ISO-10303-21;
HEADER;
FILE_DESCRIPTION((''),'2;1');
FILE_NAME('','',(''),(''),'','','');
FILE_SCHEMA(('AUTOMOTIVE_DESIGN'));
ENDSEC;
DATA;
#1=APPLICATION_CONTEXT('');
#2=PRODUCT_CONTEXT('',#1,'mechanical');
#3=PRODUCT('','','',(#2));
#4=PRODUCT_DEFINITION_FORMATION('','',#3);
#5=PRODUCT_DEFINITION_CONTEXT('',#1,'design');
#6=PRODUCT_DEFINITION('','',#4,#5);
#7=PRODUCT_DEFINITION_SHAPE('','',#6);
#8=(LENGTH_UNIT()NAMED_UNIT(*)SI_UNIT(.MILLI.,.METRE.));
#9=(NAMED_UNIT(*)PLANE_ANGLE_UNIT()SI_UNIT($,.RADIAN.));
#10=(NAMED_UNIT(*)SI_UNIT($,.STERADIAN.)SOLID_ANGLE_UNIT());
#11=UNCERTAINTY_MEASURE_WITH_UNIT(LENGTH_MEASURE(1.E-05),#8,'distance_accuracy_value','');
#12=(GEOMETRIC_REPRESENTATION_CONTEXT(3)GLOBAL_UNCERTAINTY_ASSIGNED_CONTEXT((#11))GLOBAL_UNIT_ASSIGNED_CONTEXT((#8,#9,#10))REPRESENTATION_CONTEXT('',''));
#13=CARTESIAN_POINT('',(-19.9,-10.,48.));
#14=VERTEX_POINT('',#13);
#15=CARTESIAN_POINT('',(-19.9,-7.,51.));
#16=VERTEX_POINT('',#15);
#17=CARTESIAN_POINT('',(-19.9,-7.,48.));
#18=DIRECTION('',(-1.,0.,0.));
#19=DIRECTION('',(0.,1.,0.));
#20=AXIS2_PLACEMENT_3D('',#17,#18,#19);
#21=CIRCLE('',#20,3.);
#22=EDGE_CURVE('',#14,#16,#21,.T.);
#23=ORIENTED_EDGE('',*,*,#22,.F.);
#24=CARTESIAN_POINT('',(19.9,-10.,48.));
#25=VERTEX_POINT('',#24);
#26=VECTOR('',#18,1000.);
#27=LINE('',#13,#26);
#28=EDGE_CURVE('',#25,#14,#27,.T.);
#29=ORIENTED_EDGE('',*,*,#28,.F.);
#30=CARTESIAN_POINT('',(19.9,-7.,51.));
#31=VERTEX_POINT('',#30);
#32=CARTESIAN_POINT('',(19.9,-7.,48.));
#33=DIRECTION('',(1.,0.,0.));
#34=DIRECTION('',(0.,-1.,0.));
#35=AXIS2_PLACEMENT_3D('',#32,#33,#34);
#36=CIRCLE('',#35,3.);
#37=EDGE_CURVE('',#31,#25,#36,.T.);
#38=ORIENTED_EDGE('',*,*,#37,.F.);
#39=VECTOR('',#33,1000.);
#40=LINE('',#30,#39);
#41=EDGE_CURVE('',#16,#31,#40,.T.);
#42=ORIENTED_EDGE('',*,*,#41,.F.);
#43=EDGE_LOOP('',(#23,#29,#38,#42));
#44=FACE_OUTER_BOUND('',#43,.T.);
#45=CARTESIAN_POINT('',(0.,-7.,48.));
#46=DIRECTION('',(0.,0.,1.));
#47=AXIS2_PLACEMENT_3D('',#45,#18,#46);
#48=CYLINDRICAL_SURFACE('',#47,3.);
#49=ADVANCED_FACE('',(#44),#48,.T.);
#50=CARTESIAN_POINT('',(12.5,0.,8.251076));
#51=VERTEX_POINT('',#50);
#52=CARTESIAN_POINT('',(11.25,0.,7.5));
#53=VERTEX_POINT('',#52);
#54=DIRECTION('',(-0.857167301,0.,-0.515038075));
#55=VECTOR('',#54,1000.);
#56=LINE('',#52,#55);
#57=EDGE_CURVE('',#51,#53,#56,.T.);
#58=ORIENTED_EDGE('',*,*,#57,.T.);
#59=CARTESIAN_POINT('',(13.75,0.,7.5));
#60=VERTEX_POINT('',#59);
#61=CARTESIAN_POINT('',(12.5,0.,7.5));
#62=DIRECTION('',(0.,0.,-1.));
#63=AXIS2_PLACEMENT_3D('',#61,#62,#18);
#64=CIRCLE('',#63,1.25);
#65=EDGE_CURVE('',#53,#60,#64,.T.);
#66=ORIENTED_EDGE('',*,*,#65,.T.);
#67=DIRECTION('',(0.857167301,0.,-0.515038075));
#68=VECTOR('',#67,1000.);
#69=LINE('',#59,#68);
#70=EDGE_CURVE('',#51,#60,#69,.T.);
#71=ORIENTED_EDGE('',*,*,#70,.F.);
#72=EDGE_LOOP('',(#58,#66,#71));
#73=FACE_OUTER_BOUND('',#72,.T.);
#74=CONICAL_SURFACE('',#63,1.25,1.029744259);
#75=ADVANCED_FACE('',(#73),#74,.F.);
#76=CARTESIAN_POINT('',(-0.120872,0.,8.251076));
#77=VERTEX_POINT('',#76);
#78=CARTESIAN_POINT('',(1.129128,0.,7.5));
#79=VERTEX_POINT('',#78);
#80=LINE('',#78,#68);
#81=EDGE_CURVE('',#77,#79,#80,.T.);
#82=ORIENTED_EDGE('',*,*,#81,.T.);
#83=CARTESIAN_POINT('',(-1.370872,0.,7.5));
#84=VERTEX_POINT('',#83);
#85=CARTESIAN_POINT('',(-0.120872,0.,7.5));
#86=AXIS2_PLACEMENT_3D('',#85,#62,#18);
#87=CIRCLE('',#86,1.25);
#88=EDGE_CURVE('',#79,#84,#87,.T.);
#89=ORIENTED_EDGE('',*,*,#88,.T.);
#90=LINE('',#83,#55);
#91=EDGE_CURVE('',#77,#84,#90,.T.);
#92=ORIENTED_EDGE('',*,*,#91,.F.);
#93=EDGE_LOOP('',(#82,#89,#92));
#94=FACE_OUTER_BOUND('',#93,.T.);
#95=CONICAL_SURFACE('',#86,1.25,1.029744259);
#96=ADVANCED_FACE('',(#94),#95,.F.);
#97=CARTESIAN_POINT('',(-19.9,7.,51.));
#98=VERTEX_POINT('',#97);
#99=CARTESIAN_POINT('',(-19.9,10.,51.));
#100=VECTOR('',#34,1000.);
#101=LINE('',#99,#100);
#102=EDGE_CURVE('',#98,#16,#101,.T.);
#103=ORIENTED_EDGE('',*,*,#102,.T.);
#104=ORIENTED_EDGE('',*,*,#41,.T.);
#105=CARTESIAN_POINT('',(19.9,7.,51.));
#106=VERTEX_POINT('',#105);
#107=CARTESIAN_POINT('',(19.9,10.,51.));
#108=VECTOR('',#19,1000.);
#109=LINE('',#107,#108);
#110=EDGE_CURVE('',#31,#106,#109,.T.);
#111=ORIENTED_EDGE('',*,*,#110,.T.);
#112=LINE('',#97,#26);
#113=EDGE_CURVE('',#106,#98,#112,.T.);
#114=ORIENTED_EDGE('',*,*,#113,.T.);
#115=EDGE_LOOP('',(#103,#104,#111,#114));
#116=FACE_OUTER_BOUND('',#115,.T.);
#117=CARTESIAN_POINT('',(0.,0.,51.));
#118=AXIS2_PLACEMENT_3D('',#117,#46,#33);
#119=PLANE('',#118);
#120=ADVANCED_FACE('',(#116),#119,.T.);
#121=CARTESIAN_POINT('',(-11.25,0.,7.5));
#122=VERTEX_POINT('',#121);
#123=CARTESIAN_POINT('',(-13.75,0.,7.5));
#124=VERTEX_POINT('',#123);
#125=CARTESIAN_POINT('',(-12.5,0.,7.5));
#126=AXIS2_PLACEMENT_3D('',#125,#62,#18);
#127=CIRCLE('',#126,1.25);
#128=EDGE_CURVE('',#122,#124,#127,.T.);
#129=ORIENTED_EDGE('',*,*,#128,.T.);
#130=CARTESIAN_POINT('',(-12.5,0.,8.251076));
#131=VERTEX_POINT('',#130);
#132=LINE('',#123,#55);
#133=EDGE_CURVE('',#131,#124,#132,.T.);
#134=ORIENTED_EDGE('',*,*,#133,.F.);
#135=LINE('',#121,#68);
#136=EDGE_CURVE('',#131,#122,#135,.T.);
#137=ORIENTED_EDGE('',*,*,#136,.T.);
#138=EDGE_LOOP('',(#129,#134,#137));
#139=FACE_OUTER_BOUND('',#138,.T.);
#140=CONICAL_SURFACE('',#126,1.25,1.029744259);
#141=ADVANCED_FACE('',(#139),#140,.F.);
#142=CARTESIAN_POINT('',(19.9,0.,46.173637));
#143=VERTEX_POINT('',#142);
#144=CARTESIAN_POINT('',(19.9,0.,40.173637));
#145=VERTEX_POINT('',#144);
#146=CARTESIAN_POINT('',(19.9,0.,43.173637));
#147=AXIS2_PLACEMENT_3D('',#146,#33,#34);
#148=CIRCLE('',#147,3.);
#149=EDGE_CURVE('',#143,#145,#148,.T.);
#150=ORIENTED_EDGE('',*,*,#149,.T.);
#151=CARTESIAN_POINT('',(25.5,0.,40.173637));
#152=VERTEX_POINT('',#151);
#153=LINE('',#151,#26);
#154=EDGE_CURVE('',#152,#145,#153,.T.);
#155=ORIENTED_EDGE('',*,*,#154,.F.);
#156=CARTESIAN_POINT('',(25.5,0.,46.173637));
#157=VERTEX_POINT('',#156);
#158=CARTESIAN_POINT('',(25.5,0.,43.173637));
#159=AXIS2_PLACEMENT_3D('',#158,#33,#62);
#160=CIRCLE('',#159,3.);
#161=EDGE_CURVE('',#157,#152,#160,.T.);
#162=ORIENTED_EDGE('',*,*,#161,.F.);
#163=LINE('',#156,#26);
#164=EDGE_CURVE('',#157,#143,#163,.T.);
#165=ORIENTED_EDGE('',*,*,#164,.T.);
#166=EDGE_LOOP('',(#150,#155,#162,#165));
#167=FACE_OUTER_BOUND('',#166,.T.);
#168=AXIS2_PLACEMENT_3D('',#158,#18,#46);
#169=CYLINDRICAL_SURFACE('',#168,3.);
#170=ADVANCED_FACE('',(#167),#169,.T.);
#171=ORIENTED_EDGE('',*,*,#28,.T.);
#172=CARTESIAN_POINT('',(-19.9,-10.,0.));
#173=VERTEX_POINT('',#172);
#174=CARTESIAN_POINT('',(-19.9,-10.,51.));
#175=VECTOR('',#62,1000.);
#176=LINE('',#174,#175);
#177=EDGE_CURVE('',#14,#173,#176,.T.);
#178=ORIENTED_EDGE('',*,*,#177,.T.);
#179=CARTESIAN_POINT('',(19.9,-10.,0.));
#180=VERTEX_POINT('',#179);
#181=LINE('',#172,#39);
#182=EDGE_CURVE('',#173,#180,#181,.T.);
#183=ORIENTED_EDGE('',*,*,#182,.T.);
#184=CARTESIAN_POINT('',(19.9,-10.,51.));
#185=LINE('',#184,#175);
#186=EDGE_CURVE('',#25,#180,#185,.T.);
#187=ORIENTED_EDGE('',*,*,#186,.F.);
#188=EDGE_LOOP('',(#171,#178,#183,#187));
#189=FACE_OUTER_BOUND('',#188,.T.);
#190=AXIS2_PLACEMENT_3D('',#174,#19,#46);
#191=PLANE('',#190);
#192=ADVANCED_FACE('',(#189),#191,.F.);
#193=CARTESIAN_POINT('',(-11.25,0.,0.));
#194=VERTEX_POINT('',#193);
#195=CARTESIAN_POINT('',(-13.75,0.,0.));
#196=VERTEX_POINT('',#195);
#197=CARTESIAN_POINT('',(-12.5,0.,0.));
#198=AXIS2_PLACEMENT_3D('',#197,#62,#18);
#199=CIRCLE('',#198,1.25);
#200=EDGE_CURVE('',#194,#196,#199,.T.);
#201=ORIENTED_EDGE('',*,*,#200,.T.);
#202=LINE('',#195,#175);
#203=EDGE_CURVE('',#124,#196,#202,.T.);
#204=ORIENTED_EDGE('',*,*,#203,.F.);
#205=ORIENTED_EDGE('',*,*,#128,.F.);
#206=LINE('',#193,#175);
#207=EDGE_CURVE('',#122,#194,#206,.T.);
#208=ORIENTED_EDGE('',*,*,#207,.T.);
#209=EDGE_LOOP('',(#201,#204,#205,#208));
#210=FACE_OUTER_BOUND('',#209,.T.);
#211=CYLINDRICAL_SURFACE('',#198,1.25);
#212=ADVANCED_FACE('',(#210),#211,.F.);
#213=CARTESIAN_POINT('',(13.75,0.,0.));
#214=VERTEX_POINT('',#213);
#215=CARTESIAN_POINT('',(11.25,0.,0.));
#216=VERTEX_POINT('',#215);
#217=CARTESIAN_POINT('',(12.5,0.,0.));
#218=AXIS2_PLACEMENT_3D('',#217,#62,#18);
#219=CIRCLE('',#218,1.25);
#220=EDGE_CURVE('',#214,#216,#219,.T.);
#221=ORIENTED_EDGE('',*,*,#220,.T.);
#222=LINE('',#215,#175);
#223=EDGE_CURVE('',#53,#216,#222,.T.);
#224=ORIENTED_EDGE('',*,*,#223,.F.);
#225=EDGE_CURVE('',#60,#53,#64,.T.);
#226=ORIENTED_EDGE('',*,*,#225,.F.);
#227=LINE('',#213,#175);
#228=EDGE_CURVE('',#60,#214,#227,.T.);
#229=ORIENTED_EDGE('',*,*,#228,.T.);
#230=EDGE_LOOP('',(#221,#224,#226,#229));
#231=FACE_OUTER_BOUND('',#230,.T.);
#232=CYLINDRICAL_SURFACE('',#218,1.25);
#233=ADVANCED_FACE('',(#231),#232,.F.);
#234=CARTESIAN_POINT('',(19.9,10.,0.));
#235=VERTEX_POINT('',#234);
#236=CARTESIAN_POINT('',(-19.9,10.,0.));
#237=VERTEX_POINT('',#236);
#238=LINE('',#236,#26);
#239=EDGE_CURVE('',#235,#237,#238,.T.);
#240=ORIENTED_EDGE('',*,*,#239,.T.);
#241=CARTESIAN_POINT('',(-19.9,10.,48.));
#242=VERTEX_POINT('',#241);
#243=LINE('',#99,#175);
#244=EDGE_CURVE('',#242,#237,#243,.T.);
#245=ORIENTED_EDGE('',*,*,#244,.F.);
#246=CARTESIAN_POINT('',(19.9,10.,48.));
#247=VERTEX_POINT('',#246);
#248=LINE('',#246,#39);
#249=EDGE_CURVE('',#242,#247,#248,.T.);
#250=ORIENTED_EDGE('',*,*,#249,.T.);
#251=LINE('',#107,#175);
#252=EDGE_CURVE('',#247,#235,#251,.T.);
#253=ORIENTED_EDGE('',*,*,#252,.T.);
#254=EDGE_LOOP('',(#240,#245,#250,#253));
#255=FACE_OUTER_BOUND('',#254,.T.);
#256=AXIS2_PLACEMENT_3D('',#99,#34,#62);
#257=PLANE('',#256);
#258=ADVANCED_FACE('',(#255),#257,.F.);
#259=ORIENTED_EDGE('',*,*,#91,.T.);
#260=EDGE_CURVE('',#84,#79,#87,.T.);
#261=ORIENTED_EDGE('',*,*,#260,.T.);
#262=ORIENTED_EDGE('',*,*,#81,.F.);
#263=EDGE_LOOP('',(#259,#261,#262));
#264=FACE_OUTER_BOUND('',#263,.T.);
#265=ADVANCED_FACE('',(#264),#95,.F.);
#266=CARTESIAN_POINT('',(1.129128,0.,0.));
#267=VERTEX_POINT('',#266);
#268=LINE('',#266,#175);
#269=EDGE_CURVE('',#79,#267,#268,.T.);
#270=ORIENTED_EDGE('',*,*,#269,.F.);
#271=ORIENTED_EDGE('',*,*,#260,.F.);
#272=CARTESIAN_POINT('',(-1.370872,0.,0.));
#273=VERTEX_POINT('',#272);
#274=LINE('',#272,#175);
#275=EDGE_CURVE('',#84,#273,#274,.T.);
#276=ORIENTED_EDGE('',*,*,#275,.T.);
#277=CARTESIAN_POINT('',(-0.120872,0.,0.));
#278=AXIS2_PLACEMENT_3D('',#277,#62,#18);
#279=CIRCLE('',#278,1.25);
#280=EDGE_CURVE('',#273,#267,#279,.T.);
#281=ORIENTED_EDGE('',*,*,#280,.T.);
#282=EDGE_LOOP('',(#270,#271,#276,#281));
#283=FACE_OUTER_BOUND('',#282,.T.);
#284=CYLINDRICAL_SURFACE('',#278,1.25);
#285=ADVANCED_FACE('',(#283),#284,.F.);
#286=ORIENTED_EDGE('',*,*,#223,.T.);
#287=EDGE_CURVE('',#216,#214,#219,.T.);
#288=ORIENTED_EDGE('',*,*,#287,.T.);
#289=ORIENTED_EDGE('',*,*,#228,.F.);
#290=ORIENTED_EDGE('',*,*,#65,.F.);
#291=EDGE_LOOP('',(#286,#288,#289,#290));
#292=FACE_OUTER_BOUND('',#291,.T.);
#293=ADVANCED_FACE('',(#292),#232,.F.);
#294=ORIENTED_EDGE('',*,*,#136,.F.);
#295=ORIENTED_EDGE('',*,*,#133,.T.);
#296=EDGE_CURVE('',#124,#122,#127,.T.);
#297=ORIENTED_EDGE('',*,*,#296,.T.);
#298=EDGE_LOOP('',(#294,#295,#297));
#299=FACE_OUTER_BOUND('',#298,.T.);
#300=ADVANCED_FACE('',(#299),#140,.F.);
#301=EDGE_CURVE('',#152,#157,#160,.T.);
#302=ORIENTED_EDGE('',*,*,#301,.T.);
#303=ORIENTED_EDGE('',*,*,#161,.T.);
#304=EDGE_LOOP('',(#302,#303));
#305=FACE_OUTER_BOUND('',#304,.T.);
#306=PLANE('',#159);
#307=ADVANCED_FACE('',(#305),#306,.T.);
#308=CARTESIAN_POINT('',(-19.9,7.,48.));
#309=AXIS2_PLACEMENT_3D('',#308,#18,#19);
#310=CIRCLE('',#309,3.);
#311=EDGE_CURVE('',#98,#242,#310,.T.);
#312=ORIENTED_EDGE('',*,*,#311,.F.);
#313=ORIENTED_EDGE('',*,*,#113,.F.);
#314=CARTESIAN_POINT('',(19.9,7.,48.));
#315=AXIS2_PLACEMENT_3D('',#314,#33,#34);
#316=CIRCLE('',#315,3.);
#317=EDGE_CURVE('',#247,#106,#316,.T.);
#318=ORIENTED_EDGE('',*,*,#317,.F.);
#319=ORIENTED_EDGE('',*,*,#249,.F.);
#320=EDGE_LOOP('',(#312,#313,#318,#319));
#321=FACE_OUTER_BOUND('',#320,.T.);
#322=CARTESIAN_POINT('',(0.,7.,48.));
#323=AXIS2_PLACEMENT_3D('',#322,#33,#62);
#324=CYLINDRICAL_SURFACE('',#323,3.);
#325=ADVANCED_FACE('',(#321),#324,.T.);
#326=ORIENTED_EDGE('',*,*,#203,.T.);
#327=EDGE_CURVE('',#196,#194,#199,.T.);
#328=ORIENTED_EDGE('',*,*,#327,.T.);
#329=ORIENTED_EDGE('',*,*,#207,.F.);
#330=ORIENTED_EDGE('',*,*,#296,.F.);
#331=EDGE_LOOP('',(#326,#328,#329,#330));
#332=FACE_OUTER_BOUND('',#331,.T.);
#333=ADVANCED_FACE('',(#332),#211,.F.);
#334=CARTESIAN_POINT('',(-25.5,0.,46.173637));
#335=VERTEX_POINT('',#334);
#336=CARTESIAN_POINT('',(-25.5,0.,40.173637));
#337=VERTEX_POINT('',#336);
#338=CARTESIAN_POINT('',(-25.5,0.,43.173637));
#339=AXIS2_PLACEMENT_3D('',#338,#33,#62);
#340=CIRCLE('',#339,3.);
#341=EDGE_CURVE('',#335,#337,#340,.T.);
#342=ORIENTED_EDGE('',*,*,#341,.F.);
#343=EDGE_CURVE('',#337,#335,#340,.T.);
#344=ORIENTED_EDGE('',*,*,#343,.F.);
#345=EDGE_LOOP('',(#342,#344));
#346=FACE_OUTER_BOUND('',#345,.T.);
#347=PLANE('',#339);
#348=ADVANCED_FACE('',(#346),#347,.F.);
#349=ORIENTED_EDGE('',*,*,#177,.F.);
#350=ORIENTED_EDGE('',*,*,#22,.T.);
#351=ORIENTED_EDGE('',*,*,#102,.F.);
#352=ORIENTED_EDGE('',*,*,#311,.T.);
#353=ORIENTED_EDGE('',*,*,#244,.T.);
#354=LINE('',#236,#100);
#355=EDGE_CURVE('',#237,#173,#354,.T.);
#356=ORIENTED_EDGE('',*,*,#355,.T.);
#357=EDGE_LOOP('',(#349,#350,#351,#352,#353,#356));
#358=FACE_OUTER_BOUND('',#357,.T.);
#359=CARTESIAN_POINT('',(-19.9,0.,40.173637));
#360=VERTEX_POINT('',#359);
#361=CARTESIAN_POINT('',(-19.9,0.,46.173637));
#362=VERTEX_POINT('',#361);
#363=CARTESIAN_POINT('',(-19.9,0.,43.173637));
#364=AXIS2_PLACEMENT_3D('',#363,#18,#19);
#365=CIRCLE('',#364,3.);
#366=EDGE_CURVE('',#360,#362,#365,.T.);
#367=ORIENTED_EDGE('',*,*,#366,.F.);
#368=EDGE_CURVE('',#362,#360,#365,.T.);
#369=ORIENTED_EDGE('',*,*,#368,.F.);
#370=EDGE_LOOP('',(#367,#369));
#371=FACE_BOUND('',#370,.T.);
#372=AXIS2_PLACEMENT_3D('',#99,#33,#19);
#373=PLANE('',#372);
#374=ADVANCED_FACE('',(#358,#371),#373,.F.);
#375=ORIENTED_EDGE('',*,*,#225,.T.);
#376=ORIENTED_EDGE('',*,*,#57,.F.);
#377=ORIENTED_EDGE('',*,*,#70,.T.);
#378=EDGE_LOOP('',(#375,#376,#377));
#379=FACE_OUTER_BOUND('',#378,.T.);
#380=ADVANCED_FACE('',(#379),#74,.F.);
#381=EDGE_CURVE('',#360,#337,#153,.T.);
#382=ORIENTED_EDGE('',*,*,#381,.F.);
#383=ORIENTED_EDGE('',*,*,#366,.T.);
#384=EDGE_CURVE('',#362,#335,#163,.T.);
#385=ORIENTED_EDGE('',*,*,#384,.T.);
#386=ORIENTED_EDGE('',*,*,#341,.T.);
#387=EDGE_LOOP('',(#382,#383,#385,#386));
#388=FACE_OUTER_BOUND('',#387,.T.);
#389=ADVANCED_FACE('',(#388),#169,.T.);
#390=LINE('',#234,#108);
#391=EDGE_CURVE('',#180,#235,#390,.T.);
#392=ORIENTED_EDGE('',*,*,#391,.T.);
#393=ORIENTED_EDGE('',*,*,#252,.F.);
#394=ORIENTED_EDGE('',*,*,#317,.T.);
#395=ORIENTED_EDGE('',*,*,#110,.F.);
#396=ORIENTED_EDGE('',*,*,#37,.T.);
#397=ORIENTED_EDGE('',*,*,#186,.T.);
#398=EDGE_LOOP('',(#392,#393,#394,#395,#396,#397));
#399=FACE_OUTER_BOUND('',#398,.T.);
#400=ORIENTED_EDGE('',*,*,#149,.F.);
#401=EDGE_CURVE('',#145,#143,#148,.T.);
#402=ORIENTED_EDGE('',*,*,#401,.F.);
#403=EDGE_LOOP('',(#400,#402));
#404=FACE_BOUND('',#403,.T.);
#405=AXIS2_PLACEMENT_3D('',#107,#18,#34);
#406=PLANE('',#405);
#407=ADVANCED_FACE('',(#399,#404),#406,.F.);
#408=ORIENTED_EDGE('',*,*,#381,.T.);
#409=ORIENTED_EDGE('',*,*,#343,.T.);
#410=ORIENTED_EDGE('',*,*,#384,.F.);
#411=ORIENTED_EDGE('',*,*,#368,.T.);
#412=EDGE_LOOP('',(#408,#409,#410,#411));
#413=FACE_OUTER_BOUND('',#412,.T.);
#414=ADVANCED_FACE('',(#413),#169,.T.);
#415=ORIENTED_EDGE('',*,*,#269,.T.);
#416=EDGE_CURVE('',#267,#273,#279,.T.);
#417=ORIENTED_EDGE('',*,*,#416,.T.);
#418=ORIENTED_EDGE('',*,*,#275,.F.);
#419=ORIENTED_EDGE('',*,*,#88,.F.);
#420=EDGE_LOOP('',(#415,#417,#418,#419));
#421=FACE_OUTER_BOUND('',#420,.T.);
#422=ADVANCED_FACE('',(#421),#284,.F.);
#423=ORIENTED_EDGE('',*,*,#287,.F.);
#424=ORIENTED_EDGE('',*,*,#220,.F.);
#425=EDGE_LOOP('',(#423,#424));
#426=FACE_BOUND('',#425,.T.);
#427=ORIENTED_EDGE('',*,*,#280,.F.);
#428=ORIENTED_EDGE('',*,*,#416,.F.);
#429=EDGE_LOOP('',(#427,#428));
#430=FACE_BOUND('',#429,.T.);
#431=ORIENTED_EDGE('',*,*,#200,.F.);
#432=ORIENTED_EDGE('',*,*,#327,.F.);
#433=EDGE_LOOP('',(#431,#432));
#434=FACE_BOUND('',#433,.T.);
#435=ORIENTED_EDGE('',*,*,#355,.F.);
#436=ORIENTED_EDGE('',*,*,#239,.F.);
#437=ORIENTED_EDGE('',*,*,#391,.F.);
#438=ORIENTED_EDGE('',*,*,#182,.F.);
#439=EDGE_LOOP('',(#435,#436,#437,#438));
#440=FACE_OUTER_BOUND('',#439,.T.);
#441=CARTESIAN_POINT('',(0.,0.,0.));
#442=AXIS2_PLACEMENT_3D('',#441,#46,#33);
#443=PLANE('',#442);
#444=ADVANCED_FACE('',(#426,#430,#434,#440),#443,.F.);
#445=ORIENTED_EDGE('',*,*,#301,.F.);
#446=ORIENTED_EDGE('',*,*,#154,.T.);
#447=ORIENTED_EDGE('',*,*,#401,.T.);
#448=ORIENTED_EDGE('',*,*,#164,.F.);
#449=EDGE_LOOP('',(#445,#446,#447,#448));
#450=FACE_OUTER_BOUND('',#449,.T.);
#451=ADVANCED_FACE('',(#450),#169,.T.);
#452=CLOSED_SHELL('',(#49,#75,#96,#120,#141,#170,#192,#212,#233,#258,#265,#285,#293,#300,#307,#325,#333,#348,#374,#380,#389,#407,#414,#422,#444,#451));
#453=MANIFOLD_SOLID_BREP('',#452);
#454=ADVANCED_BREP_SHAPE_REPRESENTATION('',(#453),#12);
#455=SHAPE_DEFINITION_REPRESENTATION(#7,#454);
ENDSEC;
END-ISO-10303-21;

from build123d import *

# Parameters (mm, degrees)
SKETCH1_W             = 39.8
SKETCH1_H             = 20
BOSS_EXTRUDE1_DEPTH   = 51
SKETCH2_R             = 3
BOSS_EXTRUDE2_DEPTH   = 25.5
M3_TAPPED_HOLE1_D     = 2.5
M3_TAPPED_HOLE1_DEPTH = 7.5
M3_TAPPED_HOLE1_TIP   = 0.751075774
FILLET1_R             = 3


with BuildPart() as part:
    # Sketch1 → Boss-Extrude1 (new body)
    with BuildSketch(Plane.XY):
        Rectangle(SKETCH1_W, SKETCH1_H)
    extrude(amount=BOSS_EXTRUDE1_DEPTH)

    # Sketch2 → Boss-Extrude2 (add, symmetric)
    with BuildSketch(Plane(origin=(0, 0, 0), x_dir=(0, 0, -1), z_dir=(1, 0, 0))):
        with Locations(Location((-43.173636791, 0, 0), (0, 0, 90))):
            Circle(SKETCH2_R)
    extrude(amount=BOSS_EXTRUDE2_DEPTH, both=True)

    # M3 Tapped Hole1
    with Locations(Plane(origin=(12.5, 0, 0), x_dir=(-1, 0, 0), z_dir=(0, 0, -1))):
        with Locations((0, 0), (25, 0), (12.62087232, 0)):
            Hole(M3_TAPPED_HOLE1_D / 2, depth=M3_TAPPED_HOLE1_DEPTH)
            with Locations((0, 0, -(M3_TAPPED_HOLE1_DEPTH + M3_TAPPED_HOLE1_TIP / 2))):  # 118° drill point
                Cone(0, M3_TAPPED_HOLE1_D / 2, M3_TAPPED_HOLE1_TIP, mode=Mode.SUBTRACT)

    # Fillet1
    fillet1_edges = [part.edges().sort_by_distance(p)[0] for p in [
        (0, -10, 51),
        (0, 10, 51),
    ]]
    fillet(fillet1_edges, radius=FILLET1_R)


solid = part.part
